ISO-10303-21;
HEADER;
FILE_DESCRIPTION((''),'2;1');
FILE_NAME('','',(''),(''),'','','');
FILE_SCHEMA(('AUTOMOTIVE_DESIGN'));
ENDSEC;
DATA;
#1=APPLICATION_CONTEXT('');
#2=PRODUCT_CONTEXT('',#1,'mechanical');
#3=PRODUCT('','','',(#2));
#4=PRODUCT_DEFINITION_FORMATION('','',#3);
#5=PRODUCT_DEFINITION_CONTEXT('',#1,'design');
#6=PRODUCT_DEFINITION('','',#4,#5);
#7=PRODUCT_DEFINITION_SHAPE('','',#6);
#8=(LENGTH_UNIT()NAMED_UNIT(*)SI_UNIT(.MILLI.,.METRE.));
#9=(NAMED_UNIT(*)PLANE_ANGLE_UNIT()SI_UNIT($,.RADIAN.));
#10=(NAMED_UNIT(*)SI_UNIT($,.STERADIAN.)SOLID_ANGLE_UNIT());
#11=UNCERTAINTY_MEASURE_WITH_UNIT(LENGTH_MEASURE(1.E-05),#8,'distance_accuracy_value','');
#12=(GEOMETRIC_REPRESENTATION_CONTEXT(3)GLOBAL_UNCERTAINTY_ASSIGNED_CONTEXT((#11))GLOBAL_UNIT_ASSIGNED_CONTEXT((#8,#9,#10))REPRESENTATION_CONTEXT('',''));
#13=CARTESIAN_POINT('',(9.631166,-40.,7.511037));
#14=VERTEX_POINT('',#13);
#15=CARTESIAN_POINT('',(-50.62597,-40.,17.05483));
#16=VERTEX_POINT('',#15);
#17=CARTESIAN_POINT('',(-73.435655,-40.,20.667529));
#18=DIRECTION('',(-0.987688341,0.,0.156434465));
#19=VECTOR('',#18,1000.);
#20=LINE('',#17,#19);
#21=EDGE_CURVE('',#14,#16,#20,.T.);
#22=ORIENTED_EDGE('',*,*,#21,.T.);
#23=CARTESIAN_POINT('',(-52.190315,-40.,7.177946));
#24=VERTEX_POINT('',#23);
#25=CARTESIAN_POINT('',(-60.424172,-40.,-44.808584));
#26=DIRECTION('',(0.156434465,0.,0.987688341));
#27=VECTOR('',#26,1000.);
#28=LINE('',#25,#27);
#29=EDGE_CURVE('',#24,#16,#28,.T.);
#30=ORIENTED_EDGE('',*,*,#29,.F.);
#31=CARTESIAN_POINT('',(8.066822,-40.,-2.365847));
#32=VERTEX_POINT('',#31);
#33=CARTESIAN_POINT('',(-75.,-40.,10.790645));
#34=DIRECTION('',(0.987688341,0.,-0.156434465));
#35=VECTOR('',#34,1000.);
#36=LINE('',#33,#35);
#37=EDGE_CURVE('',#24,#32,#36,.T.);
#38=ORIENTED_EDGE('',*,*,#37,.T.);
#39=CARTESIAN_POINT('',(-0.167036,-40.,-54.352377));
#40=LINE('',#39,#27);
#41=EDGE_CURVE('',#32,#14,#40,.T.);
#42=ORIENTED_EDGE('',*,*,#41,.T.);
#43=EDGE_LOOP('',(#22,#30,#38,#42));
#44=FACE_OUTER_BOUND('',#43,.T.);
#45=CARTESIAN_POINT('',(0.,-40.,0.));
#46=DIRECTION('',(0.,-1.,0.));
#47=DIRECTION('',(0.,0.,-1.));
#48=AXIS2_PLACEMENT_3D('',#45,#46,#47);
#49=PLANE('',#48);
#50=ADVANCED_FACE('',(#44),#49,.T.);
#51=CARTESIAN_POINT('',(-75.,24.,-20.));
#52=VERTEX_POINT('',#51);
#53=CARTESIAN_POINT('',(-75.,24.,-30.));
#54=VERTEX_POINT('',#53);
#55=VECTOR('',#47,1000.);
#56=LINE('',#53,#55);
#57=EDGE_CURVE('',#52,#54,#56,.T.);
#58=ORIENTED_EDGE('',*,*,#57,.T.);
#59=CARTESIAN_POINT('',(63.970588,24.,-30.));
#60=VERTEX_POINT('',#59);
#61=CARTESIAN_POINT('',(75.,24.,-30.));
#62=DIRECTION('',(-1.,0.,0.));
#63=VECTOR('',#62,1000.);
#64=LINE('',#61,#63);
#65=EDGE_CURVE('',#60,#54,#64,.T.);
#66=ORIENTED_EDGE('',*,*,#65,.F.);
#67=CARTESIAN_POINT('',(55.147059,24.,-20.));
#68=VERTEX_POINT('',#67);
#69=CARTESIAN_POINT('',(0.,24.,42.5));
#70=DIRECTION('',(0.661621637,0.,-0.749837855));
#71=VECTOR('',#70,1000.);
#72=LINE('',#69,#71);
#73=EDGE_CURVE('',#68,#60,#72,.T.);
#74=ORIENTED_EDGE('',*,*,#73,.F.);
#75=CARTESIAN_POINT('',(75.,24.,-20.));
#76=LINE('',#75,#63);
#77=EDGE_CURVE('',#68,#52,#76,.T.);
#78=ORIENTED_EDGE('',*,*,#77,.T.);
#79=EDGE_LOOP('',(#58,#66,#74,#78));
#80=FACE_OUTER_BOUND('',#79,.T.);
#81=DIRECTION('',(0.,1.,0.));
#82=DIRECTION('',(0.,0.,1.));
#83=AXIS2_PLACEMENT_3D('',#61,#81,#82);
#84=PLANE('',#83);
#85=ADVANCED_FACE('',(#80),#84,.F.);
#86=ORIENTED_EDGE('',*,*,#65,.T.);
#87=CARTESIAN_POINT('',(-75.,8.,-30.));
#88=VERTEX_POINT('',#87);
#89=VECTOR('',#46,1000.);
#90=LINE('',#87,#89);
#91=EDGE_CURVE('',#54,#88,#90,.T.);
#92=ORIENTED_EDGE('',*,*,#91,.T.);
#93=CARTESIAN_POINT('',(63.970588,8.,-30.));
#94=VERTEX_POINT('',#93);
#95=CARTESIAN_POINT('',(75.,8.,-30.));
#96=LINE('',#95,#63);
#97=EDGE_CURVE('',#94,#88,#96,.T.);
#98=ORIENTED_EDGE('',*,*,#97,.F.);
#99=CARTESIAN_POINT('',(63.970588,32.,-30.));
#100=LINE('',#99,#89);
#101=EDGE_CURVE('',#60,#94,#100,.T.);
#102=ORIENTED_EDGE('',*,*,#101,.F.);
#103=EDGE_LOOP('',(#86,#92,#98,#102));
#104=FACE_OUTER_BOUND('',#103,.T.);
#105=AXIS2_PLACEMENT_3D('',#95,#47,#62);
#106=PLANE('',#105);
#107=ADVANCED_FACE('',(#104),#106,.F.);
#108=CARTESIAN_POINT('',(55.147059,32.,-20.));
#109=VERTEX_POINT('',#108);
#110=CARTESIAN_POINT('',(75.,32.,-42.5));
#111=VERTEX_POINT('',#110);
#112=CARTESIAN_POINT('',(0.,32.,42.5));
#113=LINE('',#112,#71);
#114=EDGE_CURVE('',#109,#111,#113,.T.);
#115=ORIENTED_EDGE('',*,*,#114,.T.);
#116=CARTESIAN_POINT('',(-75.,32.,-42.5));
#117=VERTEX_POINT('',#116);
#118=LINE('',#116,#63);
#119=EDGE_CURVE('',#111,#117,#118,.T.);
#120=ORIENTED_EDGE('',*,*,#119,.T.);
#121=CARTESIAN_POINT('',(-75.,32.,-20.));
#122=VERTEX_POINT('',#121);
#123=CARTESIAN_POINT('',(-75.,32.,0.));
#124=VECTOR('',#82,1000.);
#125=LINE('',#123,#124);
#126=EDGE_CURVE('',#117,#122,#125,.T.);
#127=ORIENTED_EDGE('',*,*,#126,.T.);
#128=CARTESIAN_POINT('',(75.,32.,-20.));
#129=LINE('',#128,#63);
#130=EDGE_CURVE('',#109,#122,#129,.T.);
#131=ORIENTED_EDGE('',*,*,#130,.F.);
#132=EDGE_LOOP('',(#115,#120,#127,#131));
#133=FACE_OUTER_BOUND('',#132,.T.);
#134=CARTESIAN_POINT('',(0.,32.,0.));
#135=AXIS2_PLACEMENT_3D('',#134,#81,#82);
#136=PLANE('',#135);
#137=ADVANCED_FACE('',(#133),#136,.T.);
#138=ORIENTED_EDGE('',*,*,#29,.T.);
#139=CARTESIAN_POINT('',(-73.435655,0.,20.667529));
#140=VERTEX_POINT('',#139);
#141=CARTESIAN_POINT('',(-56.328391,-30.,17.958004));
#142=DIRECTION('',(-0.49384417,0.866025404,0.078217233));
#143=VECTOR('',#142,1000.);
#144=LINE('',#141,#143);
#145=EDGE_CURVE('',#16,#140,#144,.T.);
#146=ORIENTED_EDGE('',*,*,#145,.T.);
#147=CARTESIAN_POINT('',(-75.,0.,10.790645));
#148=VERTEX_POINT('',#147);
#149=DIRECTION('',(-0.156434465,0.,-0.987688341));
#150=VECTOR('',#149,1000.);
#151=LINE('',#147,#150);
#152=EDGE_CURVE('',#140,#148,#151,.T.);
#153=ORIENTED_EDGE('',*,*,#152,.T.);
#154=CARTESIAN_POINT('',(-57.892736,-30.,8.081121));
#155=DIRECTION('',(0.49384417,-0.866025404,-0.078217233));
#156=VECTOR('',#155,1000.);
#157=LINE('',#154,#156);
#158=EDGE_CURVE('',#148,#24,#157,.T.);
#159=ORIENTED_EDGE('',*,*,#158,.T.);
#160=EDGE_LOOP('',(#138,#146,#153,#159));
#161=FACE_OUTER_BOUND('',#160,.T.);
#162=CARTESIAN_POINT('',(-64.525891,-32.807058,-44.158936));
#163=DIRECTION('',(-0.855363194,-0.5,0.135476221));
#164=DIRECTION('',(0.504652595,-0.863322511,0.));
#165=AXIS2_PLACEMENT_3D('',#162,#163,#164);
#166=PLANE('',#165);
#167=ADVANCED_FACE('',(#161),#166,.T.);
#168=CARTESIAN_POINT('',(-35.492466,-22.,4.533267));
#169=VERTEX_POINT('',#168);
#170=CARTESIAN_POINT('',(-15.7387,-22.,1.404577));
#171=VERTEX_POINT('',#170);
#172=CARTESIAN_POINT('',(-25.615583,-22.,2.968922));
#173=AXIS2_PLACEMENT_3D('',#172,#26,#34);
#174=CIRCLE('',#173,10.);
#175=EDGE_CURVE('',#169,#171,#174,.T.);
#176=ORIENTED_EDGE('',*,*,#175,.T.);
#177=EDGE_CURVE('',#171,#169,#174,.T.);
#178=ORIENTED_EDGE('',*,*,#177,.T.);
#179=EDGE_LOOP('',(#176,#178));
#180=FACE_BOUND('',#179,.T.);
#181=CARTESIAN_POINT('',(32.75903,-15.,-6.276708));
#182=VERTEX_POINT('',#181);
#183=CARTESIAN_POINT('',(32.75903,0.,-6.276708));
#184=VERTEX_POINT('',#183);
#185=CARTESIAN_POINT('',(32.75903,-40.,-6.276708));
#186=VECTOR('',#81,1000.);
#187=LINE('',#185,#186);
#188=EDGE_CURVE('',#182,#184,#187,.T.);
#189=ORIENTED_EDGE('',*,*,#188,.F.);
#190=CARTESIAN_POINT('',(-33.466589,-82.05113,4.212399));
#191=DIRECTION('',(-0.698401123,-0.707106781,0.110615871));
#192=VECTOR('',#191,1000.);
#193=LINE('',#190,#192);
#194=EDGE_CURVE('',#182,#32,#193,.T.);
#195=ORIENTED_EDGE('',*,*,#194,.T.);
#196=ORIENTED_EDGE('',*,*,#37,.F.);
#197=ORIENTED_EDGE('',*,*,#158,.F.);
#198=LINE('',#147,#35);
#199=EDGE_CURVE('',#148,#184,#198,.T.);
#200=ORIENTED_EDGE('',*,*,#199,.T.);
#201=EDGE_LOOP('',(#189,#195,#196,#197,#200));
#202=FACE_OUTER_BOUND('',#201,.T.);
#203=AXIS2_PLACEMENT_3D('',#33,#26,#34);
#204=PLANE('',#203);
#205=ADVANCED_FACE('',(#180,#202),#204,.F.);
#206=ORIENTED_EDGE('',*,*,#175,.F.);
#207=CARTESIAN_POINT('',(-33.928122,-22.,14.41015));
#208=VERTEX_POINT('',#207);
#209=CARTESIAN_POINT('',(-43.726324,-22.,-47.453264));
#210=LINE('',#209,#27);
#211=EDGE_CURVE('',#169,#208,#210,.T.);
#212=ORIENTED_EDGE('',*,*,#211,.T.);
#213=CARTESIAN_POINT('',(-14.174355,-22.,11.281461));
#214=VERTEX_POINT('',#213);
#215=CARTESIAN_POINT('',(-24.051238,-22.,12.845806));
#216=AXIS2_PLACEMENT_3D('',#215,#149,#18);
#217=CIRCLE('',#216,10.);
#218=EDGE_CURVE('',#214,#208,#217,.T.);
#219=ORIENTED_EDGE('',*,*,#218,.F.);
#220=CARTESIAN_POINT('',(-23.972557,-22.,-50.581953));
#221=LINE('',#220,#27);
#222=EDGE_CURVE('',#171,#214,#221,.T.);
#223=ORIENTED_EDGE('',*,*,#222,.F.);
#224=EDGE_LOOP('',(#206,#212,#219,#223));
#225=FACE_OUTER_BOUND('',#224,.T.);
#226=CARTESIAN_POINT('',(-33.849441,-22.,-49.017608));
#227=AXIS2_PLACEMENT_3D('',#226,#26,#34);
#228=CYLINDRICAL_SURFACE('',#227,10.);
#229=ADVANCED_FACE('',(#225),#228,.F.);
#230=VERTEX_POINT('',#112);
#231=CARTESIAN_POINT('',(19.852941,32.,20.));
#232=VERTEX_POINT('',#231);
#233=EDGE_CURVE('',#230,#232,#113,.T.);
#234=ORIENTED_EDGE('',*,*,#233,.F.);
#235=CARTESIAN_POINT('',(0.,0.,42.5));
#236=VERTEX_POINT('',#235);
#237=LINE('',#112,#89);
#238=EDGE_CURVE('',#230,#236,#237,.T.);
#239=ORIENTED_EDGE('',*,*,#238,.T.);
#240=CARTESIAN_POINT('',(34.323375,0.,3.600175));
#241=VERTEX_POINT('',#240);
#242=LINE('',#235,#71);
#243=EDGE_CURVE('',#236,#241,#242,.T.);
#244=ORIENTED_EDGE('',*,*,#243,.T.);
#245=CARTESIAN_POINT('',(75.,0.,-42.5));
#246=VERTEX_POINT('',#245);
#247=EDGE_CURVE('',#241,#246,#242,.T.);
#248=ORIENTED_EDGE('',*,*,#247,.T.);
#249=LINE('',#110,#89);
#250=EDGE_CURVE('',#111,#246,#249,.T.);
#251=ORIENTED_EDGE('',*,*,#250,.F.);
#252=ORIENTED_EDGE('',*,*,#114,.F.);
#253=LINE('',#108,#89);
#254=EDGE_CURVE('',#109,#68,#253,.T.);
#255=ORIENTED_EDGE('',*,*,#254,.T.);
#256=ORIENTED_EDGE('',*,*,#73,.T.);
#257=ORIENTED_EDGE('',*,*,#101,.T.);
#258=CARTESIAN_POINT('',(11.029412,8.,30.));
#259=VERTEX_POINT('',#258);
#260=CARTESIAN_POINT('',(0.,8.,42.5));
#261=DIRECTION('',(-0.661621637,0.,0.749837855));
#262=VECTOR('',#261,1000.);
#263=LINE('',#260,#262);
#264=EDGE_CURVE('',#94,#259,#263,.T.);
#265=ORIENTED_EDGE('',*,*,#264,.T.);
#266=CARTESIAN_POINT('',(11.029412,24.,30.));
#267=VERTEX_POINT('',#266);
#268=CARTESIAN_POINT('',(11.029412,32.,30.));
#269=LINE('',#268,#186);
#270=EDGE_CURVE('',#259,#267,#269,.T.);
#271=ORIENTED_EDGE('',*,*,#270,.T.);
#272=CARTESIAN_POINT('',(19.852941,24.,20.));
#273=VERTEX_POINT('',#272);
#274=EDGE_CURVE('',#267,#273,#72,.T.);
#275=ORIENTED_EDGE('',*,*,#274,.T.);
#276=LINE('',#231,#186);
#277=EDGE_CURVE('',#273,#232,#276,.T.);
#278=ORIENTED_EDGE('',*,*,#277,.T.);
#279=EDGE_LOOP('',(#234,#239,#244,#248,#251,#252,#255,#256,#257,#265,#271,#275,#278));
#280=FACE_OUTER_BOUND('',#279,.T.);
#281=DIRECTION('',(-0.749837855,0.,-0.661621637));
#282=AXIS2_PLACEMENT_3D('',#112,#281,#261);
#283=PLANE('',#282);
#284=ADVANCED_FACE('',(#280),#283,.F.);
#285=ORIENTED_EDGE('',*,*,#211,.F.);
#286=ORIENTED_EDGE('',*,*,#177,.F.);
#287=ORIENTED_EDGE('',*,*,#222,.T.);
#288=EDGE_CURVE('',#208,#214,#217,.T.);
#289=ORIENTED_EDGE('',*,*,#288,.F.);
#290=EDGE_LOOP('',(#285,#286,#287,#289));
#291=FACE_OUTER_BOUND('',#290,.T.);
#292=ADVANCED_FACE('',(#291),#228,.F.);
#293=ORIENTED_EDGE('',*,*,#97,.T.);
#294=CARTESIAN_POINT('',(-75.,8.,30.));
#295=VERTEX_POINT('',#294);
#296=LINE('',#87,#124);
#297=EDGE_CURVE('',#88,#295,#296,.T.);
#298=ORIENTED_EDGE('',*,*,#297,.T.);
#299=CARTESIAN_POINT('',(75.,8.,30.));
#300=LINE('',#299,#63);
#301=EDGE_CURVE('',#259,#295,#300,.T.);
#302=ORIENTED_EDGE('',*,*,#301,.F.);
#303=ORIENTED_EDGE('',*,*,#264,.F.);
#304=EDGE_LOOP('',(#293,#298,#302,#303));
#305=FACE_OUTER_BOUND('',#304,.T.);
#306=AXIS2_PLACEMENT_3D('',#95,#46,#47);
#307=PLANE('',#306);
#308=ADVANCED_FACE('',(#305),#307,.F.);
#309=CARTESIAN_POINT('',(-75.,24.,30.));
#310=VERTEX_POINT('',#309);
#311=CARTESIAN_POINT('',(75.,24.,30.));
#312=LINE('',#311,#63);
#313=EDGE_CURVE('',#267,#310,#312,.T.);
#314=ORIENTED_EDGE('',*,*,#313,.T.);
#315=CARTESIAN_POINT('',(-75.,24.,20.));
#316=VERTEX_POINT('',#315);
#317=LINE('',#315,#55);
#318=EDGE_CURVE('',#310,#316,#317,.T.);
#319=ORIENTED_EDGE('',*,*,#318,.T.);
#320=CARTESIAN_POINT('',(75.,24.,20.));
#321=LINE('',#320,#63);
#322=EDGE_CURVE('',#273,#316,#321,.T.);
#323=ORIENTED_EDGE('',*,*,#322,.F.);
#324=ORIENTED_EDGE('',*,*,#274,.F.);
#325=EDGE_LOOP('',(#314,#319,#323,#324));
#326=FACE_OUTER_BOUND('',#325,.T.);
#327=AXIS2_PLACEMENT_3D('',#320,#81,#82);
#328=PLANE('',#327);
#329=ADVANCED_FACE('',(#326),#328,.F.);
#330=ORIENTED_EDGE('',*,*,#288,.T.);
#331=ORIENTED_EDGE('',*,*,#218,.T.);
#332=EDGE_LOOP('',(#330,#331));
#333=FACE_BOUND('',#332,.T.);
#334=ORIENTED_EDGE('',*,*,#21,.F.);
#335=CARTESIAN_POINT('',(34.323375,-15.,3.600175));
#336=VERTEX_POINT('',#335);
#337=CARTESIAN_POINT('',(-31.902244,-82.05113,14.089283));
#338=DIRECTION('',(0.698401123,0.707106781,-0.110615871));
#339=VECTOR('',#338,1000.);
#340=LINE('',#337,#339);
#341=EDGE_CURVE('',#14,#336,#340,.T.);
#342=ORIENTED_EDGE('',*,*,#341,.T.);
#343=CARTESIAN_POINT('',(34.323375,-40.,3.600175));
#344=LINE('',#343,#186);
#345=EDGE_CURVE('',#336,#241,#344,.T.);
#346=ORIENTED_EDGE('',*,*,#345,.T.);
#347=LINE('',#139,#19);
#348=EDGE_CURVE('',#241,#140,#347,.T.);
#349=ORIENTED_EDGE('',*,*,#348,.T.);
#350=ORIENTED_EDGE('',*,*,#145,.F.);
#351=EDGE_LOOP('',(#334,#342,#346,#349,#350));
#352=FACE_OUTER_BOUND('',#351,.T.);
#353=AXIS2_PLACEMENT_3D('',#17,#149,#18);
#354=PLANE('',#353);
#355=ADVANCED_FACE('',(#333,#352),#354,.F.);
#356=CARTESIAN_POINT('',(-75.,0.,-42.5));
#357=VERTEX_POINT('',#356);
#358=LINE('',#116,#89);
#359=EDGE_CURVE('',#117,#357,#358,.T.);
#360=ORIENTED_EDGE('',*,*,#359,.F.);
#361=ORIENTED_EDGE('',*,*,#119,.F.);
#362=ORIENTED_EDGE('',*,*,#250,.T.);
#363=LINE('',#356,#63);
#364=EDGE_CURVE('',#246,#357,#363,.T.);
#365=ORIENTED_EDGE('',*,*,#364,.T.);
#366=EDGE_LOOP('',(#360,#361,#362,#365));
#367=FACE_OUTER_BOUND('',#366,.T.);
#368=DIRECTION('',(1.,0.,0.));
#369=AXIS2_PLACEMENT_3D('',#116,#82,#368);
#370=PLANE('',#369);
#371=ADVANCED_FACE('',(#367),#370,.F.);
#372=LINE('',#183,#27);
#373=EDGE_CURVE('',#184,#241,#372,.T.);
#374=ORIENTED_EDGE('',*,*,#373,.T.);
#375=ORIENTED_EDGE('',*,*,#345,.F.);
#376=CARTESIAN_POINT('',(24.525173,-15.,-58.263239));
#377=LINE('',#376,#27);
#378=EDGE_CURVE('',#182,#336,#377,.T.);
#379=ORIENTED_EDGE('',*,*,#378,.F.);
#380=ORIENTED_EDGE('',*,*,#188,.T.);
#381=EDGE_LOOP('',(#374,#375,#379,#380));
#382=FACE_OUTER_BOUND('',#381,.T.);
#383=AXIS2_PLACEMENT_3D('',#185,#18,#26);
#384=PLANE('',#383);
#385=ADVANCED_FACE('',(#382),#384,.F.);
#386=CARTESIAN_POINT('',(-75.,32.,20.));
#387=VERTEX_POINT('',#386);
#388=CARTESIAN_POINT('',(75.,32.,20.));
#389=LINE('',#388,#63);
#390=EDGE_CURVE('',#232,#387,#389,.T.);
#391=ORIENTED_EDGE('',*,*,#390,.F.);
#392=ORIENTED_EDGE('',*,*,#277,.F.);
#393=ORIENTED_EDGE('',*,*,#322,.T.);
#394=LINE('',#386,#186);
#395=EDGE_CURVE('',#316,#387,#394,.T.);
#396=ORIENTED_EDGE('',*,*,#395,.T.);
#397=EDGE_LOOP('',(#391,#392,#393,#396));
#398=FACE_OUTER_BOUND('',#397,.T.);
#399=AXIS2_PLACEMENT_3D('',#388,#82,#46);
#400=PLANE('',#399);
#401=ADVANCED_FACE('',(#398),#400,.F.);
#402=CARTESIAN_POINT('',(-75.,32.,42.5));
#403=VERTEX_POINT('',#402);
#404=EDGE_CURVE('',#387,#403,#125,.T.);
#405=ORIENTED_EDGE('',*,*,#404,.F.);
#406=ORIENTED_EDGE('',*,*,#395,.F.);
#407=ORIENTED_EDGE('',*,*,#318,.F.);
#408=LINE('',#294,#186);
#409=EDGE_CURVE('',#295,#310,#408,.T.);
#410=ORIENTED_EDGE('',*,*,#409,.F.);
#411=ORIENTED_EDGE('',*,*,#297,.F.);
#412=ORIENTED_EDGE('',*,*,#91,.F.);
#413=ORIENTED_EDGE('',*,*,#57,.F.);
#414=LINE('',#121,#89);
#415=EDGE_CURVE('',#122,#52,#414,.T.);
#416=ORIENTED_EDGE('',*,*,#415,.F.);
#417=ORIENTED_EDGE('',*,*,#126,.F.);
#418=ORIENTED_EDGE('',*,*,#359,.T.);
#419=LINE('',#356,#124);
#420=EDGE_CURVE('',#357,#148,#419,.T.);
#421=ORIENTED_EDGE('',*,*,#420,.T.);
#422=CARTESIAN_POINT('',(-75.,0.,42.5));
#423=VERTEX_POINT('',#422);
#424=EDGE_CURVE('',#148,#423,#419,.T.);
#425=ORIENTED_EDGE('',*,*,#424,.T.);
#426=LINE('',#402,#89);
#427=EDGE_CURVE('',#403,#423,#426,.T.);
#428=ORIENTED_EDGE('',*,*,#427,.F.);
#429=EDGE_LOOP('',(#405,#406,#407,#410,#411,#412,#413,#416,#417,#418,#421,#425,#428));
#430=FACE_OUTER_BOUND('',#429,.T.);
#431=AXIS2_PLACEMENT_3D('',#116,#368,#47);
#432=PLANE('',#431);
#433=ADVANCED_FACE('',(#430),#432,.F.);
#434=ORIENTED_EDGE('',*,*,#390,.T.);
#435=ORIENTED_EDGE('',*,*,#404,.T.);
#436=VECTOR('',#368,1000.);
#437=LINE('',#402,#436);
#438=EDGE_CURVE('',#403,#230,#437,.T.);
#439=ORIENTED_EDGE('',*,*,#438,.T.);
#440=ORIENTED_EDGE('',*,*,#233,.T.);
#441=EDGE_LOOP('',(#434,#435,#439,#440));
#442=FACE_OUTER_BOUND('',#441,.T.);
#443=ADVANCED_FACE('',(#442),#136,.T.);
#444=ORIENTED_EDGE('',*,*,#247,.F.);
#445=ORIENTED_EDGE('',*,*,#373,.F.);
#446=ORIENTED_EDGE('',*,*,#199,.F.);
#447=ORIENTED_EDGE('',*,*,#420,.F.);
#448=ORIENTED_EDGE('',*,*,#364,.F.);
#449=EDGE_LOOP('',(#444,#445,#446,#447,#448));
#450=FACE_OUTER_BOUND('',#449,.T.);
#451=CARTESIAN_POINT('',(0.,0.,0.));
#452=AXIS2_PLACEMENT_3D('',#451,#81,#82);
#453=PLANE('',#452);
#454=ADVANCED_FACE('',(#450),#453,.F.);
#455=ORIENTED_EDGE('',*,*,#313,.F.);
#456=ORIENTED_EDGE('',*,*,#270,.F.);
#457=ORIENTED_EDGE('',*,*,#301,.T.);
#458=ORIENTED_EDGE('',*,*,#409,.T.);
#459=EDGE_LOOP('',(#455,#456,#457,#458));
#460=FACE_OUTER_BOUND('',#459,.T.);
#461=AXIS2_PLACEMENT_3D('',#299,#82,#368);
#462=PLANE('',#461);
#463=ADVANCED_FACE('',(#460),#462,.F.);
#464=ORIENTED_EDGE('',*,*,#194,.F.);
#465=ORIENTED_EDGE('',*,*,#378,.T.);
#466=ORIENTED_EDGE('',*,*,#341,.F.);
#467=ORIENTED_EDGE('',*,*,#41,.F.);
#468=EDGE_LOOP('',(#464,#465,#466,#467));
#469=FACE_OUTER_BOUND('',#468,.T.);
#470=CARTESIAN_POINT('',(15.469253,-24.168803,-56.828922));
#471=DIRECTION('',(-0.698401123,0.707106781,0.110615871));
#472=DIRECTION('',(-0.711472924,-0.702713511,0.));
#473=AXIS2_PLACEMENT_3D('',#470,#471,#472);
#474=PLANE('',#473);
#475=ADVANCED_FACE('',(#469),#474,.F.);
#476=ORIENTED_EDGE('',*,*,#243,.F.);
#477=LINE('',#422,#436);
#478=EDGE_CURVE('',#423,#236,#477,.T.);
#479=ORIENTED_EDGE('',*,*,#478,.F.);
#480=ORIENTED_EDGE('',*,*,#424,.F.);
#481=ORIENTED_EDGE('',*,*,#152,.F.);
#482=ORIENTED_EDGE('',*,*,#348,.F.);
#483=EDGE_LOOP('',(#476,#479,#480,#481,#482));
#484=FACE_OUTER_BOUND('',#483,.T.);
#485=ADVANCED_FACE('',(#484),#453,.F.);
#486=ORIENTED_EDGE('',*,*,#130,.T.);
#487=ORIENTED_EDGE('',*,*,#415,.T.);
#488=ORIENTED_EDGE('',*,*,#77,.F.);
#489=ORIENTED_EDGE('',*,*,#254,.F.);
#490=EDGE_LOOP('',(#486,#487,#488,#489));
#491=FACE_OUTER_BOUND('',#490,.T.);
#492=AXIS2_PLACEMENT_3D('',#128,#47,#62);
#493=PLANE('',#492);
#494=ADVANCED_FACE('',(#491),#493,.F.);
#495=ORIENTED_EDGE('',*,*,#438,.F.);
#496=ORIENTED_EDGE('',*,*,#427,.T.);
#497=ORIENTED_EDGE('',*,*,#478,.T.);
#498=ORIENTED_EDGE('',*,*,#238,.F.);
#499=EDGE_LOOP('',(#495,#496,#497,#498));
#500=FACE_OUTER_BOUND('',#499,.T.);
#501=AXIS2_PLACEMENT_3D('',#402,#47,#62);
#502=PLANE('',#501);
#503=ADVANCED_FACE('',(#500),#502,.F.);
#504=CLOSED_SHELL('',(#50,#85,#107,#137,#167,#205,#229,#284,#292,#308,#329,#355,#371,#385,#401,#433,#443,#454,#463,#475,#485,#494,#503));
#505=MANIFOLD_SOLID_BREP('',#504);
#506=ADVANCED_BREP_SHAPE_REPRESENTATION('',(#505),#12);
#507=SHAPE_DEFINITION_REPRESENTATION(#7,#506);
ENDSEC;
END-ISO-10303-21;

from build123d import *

# Parameters (mm, degrees)
BASE_BLOCK_150X85X32_DEPTH = 32
T_SLOT_CUT_DEPTH           = 160.154798859
T_SLOT_CUT_DEPTH_BACK      = 160.154798859
TAPERED_FOOT_BOSS_DEPTH    = 40
FOOT_RELIEF_CUT_DEPTH      = 101.347613869
FOOT_RELIEF_CUT_DEPTH_BACK = 101.347613869
FOOT_RELIEF_SKETCH_R       = 10


with BuildPart() as part:
    # Base Block Sketch → Base Block 150x85x32 (new body)
    with BuildSketch(Plane(origin=(0, 0, 0), x_dir=(1, 0, 0), z_dir=(0, 1, 0))):
        Polygon((-75, 42.5), (75, 42.5), (0, -42.5), (-75, -42.5), align=None)
    extrude(amount=BASE_BLOCK_150X85X32_DEPTH)

    # T-Slot Sketch → T-Slot Cut (cut, two sides: drawn at the far end of the back side and taken through both)
    with BuildSketch(Plane.ZY.offset(75).offset(-T_SLOT_CUT_DEPTH_BACK)):
        Polygon((-20, 32), (-20, 24), (-30, 24), (-30, 8), (30, 8), (30, 24), (20, 24), (20, 32), align=None)
    extrude(amount=T_SLOT_CUT_DEPTH + T_SLOT_CUT_DEPTH_BACK, mode=Mode.SUBTRACT)

    # Tapered Foot Sketch → Tapered Foot Boss (add)
    with BuildSketch(Plane.XZ):
        Polygon((-75, 10.790645392), (-73.43565535, 20.667528798), (34.323374911, 3.6001751), (32.759030261, -6.276708306), align=None)
    extrude(amount=TAPERED_FOOT_BOSS_DEPTH)

    # Foot Relief Sketch → Foot Relief Cut (cut, two sides: drawn at the far end of the back side and taken through both)
    with BuildSketch(Plane(origin=(1.396210415, 0, 8.815325621), x_dir=(0.9876883405951378, 0, -0.15643446504023126), z_dir=(0.15643446504023126, 0, 0.9876883405951378)).offset(-FOOT_RELIEF_CUT_DEPTH_BACK)):
        Polygon((33.337605744, -15), (8.337605744, -40), (33.337605744, -40), align=None)
        with Locations((-25.764654384, -22)):
            Circle(FOOT_RELIEF_SKETCH_R)
        Polygon((-52.670643616, -40), (-75.764654384, 0), (-75.764654384, -40), align=None)
    extrude(amount=FOOT_RELIEF_CUT_DEPTH + FOOT_RELIEF_CUT_DEPTH_BACK, mode=Mode.SUBTRACT)


solid = part.part
